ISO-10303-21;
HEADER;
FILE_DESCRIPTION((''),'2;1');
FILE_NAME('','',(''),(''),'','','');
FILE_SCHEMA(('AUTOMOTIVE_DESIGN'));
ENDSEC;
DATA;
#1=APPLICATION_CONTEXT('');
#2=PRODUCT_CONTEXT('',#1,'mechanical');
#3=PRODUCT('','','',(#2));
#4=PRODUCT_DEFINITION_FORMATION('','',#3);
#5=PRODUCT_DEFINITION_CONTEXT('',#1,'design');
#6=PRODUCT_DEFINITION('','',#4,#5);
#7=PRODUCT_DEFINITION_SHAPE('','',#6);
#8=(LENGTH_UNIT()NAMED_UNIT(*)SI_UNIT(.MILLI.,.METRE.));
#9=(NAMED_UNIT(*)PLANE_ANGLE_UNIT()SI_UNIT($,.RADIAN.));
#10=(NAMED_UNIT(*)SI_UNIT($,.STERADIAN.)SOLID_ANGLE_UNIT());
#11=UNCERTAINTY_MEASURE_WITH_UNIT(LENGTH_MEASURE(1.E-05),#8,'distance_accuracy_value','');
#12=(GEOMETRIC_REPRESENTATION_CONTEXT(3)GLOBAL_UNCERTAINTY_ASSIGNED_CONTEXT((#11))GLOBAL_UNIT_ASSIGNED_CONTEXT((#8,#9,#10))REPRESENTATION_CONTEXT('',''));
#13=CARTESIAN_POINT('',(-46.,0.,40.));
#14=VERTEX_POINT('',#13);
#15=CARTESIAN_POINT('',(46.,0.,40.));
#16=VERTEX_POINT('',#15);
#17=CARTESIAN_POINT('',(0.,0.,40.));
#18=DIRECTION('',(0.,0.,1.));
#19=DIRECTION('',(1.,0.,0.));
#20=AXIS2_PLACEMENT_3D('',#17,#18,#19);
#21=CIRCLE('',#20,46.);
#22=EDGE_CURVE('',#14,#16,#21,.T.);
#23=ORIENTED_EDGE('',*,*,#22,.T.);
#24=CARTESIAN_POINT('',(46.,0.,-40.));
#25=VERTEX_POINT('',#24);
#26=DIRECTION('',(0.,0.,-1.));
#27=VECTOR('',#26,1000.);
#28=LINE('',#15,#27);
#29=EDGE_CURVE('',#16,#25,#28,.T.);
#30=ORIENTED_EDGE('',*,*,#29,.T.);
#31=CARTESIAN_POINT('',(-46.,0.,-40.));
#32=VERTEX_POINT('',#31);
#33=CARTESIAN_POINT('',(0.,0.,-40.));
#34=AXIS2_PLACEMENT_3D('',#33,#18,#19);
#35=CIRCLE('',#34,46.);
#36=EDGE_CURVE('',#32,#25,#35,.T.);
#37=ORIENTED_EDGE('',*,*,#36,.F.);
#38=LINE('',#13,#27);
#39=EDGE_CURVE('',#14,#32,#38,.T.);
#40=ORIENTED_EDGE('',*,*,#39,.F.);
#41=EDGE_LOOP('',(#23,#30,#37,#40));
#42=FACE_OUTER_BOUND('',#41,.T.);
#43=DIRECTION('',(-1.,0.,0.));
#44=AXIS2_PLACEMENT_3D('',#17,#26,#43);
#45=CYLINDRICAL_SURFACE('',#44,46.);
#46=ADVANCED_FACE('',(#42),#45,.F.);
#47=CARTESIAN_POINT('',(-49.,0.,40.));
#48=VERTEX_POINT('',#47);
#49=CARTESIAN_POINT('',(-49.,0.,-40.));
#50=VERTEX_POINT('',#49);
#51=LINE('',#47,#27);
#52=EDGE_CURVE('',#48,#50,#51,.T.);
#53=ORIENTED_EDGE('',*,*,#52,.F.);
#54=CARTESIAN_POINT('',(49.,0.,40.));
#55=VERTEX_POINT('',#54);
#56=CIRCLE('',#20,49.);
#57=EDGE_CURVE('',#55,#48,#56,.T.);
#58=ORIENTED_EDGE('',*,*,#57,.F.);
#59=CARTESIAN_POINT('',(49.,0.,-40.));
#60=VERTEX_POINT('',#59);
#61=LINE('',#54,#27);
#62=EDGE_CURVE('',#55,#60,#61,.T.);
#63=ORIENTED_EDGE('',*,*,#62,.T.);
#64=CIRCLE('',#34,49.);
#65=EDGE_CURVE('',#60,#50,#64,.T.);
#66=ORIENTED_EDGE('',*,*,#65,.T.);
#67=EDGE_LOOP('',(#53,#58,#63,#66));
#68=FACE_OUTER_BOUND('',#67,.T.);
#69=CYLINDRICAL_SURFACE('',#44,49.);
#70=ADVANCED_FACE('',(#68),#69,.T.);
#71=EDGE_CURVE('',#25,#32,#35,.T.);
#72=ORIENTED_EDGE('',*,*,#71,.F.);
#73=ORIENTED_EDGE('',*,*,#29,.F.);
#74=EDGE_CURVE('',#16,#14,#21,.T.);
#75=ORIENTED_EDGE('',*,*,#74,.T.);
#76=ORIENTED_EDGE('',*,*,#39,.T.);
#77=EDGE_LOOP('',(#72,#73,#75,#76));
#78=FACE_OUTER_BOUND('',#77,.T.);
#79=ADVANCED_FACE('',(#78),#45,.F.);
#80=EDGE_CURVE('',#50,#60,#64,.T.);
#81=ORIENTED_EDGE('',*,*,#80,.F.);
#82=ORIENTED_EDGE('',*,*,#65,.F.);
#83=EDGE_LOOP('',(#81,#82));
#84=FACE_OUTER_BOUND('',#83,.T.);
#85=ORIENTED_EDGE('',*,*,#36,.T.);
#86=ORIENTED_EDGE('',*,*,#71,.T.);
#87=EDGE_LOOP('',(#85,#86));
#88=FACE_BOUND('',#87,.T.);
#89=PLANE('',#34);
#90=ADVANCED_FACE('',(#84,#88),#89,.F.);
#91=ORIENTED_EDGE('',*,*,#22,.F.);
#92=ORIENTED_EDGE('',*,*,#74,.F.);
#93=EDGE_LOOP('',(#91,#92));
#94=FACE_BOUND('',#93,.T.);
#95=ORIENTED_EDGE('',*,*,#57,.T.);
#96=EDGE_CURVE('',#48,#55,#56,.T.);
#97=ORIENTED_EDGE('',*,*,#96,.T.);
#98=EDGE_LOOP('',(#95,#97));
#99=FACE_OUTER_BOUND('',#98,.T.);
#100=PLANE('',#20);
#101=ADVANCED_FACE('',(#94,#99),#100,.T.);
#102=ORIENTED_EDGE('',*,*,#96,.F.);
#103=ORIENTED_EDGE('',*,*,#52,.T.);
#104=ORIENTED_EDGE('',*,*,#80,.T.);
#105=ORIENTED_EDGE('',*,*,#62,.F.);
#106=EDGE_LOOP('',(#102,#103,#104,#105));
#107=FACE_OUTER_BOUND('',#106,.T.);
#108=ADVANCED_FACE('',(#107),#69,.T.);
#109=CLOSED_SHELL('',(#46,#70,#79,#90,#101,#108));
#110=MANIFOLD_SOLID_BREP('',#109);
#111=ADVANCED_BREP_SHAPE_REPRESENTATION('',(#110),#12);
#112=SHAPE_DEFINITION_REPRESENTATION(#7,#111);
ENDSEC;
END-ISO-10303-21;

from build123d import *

# Parameters (mm, degrees)
SKETCH_1_R      = 49
SKETCH_1_R_2    = 46
EXTRUDE_1_DEPTH = 40


with BuildPart() as part:
    # 草图1 → 凸台-拉伸1 (new, symmetric)
    with BuildSketch(Plane.XY):
        Circle(SKETCH_1_R)
        Circle(SKETCH_1_R_2, mode=Mode.SUBTRACT)
    extrude(amount=EXTRUDE_1_DEPTH, both=True)


solid = part.part
